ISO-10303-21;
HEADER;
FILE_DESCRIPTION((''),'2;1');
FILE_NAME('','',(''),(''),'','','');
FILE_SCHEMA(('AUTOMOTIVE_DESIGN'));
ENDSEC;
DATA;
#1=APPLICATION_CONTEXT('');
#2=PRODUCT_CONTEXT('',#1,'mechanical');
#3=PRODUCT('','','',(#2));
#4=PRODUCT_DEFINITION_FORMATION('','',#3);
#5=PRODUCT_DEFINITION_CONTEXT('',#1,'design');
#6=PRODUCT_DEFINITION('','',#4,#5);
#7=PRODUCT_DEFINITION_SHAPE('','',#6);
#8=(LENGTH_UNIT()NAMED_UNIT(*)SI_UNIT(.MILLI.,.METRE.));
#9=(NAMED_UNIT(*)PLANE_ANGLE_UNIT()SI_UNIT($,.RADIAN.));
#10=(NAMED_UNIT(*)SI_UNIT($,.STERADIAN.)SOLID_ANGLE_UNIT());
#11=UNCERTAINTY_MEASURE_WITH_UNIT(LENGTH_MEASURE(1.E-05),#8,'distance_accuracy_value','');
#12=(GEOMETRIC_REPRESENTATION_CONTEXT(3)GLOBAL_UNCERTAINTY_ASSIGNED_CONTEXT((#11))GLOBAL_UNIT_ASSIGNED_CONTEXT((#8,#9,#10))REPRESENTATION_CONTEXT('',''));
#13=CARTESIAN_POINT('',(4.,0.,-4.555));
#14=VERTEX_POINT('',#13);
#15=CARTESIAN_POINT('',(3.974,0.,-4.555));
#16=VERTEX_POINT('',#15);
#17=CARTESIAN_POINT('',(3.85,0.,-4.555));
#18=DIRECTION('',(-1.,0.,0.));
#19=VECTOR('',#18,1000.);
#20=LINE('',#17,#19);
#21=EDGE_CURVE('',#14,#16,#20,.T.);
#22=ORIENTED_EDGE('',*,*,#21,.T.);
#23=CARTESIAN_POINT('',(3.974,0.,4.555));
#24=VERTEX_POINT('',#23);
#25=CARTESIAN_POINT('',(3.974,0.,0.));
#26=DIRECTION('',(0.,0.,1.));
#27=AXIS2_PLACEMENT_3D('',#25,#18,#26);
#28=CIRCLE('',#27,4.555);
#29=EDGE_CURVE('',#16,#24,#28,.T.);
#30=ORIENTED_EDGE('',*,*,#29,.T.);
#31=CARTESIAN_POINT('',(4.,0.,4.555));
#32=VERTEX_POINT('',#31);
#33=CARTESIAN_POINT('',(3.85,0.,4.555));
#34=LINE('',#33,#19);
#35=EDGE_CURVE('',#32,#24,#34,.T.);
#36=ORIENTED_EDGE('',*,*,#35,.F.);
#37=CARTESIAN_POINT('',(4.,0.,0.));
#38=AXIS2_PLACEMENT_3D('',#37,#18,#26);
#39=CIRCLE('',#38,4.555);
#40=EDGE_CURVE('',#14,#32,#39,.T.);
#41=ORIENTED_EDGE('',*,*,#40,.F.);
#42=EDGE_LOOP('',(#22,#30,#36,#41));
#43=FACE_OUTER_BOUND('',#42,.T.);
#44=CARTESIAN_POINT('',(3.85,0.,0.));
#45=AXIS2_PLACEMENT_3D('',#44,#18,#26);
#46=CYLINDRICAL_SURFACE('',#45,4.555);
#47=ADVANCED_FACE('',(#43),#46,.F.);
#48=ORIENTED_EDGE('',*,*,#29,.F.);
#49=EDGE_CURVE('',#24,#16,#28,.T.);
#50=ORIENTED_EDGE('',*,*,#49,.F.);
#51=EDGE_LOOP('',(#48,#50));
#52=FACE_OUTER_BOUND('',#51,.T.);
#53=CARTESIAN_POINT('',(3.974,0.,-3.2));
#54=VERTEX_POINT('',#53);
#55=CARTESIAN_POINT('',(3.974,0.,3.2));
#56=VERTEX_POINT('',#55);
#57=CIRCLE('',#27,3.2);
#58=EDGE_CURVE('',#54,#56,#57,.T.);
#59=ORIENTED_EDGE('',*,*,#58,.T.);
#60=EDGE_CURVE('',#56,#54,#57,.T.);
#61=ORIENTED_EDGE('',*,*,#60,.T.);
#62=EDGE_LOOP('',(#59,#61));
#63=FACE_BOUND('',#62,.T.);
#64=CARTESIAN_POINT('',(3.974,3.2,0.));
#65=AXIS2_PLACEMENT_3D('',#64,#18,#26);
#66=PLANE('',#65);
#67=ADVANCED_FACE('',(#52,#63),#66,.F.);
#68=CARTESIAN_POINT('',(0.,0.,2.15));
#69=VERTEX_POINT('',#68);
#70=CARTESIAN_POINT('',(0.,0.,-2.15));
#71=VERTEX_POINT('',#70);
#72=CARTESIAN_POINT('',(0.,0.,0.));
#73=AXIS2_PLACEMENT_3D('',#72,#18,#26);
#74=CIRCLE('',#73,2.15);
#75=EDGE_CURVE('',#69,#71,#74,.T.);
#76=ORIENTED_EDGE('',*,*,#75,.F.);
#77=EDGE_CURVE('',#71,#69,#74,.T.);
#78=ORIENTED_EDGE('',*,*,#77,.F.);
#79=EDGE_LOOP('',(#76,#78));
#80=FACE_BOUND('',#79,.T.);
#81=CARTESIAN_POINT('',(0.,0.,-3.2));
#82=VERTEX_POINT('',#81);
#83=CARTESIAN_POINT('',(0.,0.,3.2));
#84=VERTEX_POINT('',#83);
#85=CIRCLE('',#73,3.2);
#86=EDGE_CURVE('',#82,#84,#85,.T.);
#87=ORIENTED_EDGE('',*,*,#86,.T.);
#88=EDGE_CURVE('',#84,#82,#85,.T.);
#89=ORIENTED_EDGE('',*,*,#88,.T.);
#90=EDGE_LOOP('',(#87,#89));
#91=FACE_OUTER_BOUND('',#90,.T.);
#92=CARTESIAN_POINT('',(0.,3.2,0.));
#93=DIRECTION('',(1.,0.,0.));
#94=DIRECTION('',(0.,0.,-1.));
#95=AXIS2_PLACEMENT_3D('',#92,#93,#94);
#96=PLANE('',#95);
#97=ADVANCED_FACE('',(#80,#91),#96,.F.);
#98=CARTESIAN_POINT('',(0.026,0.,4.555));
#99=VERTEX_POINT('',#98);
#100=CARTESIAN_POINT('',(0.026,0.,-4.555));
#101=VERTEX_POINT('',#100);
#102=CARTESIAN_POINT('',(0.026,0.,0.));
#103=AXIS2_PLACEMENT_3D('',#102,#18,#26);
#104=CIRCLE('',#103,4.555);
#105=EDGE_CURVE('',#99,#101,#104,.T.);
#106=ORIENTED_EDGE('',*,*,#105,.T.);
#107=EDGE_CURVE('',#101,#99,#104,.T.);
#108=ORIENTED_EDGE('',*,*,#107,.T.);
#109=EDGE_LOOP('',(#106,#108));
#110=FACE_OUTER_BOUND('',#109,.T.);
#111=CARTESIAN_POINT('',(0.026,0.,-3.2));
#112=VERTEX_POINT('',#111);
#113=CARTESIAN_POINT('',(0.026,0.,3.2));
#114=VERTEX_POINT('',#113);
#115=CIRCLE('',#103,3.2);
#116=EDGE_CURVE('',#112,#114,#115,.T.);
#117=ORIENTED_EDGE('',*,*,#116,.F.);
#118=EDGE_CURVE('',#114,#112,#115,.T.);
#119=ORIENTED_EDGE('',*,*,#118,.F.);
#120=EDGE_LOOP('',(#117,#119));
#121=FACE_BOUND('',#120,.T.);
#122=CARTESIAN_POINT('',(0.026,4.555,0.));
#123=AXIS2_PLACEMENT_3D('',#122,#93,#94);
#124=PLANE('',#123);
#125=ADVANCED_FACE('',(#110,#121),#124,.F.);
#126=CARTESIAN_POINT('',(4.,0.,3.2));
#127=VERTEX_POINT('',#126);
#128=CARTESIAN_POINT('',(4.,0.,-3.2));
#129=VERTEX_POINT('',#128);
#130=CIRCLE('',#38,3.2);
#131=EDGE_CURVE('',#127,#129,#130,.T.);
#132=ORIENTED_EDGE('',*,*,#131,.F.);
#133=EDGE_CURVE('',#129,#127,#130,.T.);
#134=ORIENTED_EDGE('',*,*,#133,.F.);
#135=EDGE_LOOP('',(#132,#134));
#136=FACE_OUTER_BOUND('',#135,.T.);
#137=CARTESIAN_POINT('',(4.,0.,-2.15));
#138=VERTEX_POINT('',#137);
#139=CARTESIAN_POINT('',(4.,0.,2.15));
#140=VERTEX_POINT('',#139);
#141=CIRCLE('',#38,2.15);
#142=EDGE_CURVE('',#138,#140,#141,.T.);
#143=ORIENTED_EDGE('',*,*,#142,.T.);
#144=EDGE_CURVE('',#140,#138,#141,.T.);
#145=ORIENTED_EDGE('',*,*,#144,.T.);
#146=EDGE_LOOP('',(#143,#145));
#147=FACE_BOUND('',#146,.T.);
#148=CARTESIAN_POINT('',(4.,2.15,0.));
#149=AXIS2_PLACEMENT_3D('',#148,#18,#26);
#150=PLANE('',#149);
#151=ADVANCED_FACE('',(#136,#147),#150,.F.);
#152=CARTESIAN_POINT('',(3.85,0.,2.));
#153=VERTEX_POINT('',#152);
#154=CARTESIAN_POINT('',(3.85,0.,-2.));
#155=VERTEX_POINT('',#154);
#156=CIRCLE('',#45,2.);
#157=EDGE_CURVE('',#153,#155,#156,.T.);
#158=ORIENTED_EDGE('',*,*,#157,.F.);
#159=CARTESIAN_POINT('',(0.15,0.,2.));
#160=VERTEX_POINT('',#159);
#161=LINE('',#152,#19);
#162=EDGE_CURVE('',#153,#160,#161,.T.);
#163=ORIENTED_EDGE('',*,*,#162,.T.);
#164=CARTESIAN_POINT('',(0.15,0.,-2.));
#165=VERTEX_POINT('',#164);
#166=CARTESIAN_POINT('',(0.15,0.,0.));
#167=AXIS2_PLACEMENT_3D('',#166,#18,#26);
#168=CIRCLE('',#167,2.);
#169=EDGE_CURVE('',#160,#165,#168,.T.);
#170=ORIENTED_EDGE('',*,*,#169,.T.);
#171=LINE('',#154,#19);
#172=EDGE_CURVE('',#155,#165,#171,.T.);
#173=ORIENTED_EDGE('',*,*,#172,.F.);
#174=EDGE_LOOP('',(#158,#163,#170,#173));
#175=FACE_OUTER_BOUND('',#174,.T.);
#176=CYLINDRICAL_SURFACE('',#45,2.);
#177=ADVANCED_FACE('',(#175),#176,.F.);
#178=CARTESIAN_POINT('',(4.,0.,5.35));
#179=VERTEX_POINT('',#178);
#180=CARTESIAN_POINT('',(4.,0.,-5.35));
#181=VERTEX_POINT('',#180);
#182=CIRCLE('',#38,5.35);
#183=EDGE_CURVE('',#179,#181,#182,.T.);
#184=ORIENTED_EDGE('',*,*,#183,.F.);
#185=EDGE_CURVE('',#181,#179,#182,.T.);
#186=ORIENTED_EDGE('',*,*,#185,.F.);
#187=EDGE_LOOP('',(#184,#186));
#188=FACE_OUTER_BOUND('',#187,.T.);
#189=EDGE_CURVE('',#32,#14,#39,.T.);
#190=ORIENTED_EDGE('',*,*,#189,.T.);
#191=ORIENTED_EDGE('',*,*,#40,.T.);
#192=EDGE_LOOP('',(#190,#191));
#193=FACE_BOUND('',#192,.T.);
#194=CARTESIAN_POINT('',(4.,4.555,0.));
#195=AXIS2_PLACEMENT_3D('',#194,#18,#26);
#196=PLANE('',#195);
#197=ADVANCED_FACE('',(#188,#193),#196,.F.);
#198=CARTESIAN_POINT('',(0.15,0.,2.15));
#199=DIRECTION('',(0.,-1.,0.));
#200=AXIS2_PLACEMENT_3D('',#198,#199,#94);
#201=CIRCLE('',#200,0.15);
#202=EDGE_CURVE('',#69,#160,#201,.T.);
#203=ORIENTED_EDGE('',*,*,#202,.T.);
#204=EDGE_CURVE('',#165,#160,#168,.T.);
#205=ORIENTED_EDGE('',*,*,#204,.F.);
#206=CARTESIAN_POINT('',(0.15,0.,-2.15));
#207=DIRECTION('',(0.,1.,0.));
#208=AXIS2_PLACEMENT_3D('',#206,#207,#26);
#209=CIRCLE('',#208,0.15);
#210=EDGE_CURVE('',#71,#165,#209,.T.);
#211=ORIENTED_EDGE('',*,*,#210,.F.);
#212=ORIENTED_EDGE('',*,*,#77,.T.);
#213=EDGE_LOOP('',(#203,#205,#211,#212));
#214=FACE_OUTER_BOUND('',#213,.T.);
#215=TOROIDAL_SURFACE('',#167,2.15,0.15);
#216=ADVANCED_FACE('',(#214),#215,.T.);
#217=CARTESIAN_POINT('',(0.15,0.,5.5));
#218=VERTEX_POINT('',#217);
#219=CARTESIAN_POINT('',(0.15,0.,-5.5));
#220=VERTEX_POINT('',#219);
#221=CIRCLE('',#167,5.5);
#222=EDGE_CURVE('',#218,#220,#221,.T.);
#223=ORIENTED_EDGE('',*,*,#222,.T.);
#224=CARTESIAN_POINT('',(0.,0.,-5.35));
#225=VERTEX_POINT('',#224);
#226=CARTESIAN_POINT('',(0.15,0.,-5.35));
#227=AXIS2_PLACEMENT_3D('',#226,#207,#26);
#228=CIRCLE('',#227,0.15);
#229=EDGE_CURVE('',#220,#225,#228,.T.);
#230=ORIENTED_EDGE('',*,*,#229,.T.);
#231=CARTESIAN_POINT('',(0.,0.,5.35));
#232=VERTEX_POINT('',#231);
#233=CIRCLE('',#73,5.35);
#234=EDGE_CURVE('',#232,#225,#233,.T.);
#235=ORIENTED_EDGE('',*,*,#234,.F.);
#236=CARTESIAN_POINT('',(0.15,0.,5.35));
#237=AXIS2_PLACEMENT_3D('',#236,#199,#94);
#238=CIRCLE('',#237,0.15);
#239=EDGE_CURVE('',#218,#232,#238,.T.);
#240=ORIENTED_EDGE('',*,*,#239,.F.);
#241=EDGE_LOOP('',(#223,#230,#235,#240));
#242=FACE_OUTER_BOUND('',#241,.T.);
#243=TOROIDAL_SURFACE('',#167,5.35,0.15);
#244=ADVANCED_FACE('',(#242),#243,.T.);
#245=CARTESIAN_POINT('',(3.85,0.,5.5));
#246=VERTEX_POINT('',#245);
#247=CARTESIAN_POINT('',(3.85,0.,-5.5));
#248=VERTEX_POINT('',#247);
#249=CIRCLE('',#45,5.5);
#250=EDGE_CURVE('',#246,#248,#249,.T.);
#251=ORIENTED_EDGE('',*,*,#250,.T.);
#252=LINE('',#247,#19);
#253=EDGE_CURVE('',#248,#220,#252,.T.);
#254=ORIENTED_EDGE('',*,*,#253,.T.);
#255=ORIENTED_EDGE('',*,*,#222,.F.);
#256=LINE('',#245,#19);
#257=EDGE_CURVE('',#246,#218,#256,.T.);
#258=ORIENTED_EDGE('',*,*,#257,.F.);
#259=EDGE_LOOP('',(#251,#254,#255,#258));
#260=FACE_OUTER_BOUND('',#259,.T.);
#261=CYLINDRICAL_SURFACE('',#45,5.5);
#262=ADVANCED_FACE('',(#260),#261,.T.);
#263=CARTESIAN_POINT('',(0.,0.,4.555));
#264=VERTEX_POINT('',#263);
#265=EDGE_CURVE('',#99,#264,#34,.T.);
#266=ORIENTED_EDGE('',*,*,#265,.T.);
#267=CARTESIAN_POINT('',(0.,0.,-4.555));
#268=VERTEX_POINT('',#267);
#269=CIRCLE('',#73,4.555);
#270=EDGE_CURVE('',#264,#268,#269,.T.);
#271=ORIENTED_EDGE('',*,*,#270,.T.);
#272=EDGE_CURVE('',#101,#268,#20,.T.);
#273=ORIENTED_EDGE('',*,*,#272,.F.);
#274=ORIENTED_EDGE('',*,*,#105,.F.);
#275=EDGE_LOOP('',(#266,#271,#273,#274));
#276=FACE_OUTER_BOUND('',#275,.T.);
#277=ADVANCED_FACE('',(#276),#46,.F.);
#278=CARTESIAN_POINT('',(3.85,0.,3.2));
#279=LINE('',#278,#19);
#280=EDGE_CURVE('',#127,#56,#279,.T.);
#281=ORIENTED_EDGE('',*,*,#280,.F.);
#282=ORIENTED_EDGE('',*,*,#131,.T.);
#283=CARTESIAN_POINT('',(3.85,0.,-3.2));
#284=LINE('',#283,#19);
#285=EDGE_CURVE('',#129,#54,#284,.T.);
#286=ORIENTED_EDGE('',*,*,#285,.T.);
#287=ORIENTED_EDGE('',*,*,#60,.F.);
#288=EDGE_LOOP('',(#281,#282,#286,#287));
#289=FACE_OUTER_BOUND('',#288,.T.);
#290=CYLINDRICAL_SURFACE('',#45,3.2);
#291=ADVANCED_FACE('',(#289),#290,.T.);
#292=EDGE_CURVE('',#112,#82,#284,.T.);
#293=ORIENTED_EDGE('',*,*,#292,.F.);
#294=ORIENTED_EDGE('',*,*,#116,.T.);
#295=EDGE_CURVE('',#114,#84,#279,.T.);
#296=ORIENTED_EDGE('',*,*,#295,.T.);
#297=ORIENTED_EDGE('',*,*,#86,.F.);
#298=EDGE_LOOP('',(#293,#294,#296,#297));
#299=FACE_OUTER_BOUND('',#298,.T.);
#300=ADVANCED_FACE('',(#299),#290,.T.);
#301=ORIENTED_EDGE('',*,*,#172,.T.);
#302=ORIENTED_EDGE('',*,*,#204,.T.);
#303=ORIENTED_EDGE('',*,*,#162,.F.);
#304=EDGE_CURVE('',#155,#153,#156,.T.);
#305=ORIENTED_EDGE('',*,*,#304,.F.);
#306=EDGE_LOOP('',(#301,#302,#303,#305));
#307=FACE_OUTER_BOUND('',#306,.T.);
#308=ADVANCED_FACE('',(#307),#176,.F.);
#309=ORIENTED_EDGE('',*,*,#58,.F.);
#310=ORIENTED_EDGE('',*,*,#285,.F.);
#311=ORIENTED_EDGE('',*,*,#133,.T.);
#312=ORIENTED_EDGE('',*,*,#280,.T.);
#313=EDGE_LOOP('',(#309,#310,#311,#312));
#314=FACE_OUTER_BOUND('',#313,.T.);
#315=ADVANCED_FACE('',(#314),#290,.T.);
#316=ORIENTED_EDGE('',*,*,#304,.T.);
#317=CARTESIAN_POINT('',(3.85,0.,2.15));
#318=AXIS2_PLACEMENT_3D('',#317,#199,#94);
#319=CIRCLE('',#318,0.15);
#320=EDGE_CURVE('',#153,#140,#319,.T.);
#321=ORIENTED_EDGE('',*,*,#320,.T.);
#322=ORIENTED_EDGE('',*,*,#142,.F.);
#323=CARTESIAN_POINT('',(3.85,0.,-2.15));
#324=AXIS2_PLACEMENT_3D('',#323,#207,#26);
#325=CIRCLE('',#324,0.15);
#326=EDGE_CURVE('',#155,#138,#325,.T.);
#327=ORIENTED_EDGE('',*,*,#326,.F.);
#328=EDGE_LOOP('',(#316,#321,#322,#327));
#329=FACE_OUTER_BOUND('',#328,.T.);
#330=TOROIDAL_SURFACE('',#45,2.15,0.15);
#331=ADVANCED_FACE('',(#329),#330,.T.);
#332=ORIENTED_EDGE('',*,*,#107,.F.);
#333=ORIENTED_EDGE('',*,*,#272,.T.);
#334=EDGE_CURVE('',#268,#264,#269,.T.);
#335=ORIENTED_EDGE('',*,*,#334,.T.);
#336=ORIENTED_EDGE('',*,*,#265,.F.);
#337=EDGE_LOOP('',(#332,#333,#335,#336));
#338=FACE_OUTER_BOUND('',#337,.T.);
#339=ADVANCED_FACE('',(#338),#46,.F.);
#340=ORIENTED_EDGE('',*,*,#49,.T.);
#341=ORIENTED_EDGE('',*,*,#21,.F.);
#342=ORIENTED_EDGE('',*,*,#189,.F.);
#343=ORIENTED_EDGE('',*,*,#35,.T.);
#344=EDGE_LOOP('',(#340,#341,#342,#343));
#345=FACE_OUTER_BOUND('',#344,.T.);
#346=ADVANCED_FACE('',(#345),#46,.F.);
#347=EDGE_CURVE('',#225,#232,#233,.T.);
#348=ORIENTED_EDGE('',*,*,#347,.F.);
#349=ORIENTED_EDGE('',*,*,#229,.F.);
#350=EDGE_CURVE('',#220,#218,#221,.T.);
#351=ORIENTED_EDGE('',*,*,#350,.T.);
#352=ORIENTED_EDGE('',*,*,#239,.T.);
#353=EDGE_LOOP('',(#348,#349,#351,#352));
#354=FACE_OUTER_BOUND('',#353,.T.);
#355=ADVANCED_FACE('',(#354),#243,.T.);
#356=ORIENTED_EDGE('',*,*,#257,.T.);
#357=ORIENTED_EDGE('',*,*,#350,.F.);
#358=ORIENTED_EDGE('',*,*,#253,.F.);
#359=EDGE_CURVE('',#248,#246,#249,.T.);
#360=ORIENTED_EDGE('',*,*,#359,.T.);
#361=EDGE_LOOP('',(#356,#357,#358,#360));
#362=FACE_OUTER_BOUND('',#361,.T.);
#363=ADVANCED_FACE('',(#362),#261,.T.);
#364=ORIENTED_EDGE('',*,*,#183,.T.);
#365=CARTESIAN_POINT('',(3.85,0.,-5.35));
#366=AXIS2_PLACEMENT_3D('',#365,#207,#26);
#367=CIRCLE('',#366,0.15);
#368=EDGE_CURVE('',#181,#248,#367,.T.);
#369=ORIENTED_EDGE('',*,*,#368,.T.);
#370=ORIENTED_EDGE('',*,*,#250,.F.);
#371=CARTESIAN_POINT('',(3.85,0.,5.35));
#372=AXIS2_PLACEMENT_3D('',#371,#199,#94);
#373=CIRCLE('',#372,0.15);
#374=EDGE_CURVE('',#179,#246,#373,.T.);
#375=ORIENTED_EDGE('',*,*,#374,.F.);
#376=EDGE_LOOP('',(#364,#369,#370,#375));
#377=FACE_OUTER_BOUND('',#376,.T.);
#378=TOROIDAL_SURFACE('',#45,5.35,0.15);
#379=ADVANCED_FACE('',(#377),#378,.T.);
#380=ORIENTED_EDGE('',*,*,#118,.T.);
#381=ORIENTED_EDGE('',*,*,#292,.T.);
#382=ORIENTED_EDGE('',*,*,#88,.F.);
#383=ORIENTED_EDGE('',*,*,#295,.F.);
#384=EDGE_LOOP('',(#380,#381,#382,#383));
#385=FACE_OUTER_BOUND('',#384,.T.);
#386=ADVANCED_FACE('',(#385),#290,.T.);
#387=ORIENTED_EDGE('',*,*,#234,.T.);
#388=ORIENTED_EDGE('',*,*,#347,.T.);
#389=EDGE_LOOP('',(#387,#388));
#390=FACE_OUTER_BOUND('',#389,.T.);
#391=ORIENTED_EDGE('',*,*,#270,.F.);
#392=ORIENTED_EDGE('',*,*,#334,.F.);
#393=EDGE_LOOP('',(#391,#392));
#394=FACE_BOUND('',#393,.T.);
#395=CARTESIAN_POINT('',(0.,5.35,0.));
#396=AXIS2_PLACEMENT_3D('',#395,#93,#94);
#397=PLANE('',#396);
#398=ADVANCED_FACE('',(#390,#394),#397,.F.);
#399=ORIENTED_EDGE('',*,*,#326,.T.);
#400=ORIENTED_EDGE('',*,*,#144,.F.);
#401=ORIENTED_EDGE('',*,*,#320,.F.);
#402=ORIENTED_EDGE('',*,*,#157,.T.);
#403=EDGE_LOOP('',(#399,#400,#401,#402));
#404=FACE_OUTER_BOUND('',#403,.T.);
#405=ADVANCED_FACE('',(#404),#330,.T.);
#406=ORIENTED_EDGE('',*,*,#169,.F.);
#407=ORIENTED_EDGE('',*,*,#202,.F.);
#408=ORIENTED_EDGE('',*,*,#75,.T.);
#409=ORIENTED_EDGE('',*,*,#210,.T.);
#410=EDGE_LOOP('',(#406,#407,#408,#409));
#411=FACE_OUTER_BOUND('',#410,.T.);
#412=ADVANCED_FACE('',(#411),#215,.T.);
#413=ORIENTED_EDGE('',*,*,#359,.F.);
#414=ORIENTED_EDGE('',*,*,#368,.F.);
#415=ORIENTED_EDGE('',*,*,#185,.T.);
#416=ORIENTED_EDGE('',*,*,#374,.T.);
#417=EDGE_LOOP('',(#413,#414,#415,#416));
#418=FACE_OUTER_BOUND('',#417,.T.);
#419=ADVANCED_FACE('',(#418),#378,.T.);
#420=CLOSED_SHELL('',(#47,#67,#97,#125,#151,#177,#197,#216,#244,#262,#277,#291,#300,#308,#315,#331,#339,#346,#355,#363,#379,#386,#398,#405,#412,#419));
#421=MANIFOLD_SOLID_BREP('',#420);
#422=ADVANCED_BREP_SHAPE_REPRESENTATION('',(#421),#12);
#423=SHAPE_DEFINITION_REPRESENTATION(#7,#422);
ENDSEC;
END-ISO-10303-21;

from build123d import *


with BuildPart() as part:
    # 草图1 → 旋转1 (revolve)
    with BuildSketch(Plane.XY, mode=Mode.PRIVATE) as revolve_1_sk:
        with BuildLine():
            Line((0, 5.35), (0, 4.555))
            Line((0, 4.555), (0.026, 4.555))
            Line((0.026, 4.555), (0.026, 3.2))
            Line((0.026, 3.2), (0, 3.2))
            Line((0, 3.2), (0, 2.15))
            ThreePointArc((0, 2.15), (0.043933983, 2.043933983), (0.15, 2))
            Line((0.15, 2), (3.85, 2))
            ThreePointArc((3.85, 2), (3.956066017, 2.043933983), (4, 2.15))
            Line((4, 2.15), (4, 3.2))
            Line((4, 3.2), (3.974, 3.2))
            Line((3.974, 3.2), (3.974, 4.555))
            Line((3.974, 4.555), (4, 4.555))
            Line((4, 4.555), (4, 5.35))
            ThreePointArc((4, 5.35), (3.956066017, 5.456066017), (3.85, 5.5))
            Line((3.85, 5.5), (0.15, 5.5))
            ThreePointArc((0.15, 5.5), (0.043933983, 5.456066017), (0, 5.35))
        make_face()
    revolve(revolve_1_sk.sketch.rotate(Axis((3.85, 0, 0), (-1, 0, 0)), 270), axis=Axis((3.85, 0, 0), (-1, 0, 0)))


solid = part.part
